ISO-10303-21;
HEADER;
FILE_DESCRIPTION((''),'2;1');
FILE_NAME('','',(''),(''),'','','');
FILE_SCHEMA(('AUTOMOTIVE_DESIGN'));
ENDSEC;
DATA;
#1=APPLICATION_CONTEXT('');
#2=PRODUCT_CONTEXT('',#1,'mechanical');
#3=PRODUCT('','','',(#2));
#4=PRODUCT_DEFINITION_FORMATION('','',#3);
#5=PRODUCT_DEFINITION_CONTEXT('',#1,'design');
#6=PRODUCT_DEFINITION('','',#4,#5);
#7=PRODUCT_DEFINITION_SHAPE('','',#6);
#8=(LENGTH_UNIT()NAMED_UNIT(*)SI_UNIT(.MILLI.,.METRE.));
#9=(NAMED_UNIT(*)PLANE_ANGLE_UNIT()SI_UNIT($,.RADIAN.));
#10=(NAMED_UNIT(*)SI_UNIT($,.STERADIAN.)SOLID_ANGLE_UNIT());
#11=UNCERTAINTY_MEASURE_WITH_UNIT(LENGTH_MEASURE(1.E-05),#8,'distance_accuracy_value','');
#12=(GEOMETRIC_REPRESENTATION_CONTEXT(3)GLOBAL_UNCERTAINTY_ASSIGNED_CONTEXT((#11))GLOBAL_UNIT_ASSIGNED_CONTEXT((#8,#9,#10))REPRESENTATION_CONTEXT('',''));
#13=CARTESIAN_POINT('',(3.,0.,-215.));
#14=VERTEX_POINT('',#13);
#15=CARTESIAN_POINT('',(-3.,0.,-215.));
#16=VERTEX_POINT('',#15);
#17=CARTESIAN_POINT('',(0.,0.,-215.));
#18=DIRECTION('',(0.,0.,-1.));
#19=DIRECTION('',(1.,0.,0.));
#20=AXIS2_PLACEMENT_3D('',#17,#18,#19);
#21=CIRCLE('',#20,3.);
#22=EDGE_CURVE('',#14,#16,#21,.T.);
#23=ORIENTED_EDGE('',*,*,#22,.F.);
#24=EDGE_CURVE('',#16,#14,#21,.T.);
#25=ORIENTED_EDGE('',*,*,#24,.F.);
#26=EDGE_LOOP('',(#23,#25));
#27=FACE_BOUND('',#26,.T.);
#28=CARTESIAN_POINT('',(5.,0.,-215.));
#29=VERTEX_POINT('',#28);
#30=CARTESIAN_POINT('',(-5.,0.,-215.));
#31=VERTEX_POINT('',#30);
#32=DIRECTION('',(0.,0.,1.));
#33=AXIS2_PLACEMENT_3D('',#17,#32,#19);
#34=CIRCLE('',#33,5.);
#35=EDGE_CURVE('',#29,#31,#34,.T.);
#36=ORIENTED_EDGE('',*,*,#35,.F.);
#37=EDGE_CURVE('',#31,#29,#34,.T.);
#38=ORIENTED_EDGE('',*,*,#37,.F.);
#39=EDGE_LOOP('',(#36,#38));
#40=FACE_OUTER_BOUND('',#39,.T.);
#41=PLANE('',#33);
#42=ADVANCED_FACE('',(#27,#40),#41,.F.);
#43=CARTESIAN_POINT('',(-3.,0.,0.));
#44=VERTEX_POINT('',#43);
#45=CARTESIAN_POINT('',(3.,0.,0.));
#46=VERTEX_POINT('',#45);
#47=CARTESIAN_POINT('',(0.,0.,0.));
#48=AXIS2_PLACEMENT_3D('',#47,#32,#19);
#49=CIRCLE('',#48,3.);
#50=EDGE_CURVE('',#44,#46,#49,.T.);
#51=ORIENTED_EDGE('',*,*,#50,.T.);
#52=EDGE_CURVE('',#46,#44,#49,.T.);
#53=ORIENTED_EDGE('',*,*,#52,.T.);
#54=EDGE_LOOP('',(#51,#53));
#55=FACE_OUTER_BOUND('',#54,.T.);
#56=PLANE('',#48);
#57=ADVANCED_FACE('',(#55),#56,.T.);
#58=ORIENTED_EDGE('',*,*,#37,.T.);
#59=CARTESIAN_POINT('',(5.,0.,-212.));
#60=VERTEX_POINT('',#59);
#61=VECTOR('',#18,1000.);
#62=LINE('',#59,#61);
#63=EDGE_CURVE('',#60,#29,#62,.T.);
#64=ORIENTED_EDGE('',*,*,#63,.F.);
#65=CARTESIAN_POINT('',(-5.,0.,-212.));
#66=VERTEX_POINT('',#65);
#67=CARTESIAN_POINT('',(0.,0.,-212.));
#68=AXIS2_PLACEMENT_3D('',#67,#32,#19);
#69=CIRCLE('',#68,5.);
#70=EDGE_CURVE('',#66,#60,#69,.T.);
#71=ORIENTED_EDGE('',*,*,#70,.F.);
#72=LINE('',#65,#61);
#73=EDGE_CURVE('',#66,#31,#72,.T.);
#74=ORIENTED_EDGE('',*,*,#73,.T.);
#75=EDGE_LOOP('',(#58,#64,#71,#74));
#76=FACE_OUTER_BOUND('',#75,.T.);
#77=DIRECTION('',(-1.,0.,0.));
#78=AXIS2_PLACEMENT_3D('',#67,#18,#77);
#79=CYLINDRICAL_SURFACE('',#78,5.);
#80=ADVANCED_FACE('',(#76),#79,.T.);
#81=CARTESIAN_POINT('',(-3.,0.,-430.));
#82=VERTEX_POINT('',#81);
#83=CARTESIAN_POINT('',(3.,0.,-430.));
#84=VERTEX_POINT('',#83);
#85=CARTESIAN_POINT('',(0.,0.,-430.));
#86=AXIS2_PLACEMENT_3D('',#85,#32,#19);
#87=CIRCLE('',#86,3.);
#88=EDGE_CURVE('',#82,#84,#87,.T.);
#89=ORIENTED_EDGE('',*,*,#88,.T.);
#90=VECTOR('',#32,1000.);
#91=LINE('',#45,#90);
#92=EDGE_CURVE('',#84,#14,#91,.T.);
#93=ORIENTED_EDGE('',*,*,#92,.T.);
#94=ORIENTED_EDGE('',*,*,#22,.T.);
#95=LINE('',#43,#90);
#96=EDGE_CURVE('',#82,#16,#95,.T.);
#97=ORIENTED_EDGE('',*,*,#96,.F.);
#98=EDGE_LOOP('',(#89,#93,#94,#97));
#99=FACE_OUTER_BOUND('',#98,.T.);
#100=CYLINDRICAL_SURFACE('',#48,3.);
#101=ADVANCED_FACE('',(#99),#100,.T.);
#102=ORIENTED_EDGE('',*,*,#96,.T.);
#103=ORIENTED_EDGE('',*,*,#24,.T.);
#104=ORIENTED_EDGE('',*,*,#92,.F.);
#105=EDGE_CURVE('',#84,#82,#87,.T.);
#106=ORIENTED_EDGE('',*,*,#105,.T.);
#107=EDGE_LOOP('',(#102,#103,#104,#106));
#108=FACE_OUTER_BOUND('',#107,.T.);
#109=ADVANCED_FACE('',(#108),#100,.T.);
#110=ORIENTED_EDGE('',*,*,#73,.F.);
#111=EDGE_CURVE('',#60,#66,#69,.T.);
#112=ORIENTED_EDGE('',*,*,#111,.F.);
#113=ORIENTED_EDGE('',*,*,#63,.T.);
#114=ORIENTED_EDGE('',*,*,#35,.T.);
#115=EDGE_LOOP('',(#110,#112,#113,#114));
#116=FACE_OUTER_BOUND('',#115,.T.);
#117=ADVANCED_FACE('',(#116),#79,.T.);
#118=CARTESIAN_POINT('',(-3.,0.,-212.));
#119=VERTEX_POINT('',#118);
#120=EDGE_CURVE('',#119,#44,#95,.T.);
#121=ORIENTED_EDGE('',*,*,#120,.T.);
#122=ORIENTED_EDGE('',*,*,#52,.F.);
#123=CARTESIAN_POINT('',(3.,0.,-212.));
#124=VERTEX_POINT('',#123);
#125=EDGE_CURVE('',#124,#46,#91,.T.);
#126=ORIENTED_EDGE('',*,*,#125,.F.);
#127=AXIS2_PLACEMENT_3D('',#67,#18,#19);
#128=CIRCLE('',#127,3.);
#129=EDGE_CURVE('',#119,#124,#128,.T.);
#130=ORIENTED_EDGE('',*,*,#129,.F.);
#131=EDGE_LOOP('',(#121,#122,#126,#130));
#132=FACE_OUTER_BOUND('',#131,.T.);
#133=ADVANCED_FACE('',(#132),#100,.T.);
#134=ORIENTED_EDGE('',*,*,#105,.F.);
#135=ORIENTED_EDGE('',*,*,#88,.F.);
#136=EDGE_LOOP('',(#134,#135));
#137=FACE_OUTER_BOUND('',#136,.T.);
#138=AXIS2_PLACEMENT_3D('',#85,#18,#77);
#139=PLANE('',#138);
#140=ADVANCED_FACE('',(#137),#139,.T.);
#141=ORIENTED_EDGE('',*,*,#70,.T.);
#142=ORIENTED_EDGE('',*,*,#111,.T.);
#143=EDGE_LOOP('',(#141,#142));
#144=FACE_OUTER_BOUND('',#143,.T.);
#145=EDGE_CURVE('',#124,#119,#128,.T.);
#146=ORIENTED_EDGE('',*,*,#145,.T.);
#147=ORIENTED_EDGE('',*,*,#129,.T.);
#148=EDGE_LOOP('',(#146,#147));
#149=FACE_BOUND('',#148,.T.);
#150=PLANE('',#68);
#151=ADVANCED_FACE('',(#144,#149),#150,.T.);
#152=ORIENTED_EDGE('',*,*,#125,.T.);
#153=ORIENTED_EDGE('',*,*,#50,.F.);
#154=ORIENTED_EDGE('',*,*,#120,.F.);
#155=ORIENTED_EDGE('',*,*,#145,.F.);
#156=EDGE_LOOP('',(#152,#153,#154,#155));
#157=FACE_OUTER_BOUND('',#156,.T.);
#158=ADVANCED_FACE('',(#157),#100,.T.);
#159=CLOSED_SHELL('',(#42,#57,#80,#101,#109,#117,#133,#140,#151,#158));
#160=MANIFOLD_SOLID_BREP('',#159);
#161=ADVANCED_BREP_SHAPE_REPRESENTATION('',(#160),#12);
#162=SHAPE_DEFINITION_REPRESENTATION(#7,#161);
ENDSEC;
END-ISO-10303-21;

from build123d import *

# Parameters (mm, degrees)
SKETCH_1_W      = 3
SKETCH_1_H      = 430
EXTRUDE_START   = -215
SKETCH_3_R      = 5
EXTRUDE_1_DEPTH = 3


with BuildPart() as part:
    # 草图1 → 旋转1 (revolve)
    with BuildSketch(Plane(origin=(0, 0, 0), x_dir=(1, 0, 0), z_dir=(0, 1, 0))):
        with Locations((1.5, 215)):
            Rectangle(SKETCH_1_W, SKETCH_1_H)
    revolve(axis=Axis((0, 0, 0), (0, 0, -1)))

    # 草图3 → 凸台-拉伸1 (add)
    with BuildSketch(Plane.XY.offset(EXTRUDE_START)):
        Circle(SKETCH_3_R)
    extrude(amount=EXTRUDE_1_DEPTH)


solid = part.part
